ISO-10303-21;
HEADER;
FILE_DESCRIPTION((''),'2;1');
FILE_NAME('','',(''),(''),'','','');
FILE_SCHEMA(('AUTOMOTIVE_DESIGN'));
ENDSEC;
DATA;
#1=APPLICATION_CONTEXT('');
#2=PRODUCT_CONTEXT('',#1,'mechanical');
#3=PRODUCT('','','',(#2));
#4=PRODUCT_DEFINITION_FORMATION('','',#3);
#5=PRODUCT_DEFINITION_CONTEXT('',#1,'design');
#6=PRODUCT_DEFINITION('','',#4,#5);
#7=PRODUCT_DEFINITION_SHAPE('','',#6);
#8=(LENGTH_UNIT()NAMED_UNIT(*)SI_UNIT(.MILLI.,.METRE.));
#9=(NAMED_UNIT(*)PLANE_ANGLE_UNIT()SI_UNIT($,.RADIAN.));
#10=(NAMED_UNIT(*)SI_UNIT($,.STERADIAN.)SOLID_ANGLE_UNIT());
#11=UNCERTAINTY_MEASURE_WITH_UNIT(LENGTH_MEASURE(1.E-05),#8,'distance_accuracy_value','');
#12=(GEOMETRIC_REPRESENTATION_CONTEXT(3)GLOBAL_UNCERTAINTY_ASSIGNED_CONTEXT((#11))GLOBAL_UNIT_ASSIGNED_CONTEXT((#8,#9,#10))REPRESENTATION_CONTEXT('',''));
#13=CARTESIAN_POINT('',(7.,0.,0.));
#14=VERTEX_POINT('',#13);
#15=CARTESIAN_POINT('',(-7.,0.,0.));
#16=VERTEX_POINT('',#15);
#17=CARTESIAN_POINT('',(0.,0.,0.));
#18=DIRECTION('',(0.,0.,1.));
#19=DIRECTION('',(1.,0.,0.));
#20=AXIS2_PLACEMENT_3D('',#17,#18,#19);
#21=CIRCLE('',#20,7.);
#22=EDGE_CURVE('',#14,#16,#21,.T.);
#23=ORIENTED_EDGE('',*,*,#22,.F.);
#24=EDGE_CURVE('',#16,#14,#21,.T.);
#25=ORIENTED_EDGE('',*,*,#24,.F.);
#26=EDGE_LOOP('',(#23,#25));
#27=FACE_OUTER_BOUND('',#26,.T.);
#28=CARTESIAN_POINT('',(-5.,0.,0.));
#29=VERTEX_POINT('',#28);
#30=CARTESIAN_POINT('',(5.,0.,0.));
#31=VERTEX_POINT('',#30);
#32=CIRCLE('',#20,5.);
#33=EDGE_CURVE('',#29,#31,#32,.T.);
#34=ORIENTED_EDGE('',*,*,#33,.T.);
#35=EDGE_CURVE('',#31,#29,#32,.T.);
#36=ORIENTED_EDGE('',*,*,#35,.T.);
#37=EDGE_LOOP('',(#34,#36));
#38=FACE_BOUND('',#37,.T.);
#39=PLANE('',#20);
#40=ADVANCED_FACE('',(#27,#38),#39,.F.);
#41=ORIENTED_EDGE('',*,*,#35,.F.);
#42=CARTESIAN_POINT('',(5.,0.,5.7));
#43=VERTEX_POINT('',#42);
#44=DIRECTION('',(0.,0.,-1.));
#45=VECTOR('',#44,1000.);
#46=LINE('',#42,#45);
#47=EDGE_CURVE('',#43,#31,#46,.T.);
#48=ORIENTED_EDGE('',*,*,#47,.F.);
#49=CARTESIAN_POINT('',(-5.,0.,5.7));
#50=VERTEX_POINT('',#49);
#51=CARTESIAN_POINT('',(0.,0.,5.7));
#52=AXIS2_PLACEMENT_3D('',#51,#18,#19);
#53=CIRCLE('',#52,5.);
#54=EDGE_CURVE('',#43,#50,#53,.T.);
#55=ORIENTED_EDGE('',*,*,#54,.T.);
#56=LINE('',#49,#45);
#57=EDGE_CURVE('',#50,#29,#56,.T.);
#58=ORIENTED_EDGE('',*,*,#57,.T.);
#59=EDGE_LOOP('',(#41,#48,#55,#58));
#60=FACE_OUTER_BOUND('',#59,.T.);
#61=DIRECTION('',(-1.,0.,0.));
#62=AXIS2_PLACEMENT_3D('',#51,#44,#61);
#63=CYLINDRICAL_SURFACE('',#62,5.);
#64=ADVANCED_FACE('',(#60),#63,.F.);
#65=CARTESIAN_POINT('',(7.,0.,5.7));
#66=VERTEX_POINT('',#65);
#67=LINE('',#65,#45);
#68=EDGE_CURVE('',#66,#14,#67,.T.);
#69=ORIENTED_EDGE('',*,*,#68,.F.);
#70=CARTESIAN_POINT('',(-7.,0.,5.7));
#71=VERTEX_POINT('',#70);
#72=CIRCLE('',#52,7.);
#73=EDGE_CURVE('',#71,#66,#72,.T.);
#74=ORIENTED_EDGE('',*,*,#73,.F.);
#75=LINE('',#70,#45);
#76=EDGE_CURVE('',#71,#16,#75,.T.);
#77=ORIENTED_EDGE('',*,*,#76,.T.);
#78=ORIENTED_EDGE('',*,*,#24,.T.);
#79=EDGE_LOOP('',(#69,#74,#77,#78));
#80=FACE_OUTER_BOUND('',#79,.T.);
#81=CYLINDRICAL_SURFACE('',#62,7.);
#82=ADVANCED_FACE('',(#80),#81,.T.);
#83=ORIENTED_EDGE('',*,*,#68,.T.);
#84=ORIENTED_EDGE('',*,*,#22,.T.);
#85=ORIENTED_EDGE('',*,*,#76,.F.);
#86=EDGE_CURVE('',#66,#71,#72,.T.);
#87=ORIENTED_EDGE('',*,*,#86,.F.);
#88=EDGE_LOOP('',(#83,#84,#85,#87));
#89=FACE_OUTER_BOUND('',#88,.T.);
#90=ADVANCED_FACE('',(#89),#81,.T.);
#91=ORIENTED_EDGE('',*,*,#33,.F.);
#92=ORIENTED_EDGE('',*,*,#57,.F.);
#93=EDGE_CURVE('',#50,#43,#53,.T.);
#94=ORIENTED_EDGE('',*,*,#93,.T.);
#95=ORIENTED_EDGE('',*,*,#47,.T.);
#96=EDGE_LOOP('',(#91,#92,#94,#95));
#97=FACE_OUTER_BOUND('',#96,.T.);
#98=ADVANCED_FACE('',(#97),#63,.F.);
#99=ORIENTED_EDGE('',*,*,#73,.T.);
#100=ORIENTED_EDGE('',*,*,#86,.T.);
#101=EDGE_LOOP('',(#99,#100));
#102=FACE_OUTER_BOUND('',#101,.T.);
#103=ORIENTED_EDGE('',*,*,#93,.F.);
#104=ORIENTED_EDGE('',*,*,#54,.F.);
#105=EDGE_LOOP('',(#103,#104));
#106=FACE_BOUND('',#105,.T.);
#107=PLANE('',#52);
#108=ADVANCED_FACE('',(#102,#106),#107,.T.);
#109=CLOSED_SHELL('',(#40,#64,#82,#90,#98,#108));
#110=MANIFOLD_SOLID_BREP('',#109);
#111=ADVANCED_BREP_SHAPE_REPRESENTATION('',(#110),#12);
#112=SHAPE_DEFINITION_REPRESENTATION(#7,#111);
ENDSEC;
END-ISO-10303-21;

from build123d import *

# Parameters (mm, degrees)
SKETCH_1_R      = 7
SKETCH_1_R_2    = 5
EXTRUDE_1_DEPTH = 5.7


with BuildPart() as part:
    # 草图1 → 凸台-拉伸1 (new body)
    with BuildSketch(Plane.XY):
        Circle(SKETCH_1_R)
        Circle(SKETCH_1_R_2, mode=Mode.SUBTRACT)
    extrude(amount=EXTRUDE_1_DEPTH)


solid = part.part
